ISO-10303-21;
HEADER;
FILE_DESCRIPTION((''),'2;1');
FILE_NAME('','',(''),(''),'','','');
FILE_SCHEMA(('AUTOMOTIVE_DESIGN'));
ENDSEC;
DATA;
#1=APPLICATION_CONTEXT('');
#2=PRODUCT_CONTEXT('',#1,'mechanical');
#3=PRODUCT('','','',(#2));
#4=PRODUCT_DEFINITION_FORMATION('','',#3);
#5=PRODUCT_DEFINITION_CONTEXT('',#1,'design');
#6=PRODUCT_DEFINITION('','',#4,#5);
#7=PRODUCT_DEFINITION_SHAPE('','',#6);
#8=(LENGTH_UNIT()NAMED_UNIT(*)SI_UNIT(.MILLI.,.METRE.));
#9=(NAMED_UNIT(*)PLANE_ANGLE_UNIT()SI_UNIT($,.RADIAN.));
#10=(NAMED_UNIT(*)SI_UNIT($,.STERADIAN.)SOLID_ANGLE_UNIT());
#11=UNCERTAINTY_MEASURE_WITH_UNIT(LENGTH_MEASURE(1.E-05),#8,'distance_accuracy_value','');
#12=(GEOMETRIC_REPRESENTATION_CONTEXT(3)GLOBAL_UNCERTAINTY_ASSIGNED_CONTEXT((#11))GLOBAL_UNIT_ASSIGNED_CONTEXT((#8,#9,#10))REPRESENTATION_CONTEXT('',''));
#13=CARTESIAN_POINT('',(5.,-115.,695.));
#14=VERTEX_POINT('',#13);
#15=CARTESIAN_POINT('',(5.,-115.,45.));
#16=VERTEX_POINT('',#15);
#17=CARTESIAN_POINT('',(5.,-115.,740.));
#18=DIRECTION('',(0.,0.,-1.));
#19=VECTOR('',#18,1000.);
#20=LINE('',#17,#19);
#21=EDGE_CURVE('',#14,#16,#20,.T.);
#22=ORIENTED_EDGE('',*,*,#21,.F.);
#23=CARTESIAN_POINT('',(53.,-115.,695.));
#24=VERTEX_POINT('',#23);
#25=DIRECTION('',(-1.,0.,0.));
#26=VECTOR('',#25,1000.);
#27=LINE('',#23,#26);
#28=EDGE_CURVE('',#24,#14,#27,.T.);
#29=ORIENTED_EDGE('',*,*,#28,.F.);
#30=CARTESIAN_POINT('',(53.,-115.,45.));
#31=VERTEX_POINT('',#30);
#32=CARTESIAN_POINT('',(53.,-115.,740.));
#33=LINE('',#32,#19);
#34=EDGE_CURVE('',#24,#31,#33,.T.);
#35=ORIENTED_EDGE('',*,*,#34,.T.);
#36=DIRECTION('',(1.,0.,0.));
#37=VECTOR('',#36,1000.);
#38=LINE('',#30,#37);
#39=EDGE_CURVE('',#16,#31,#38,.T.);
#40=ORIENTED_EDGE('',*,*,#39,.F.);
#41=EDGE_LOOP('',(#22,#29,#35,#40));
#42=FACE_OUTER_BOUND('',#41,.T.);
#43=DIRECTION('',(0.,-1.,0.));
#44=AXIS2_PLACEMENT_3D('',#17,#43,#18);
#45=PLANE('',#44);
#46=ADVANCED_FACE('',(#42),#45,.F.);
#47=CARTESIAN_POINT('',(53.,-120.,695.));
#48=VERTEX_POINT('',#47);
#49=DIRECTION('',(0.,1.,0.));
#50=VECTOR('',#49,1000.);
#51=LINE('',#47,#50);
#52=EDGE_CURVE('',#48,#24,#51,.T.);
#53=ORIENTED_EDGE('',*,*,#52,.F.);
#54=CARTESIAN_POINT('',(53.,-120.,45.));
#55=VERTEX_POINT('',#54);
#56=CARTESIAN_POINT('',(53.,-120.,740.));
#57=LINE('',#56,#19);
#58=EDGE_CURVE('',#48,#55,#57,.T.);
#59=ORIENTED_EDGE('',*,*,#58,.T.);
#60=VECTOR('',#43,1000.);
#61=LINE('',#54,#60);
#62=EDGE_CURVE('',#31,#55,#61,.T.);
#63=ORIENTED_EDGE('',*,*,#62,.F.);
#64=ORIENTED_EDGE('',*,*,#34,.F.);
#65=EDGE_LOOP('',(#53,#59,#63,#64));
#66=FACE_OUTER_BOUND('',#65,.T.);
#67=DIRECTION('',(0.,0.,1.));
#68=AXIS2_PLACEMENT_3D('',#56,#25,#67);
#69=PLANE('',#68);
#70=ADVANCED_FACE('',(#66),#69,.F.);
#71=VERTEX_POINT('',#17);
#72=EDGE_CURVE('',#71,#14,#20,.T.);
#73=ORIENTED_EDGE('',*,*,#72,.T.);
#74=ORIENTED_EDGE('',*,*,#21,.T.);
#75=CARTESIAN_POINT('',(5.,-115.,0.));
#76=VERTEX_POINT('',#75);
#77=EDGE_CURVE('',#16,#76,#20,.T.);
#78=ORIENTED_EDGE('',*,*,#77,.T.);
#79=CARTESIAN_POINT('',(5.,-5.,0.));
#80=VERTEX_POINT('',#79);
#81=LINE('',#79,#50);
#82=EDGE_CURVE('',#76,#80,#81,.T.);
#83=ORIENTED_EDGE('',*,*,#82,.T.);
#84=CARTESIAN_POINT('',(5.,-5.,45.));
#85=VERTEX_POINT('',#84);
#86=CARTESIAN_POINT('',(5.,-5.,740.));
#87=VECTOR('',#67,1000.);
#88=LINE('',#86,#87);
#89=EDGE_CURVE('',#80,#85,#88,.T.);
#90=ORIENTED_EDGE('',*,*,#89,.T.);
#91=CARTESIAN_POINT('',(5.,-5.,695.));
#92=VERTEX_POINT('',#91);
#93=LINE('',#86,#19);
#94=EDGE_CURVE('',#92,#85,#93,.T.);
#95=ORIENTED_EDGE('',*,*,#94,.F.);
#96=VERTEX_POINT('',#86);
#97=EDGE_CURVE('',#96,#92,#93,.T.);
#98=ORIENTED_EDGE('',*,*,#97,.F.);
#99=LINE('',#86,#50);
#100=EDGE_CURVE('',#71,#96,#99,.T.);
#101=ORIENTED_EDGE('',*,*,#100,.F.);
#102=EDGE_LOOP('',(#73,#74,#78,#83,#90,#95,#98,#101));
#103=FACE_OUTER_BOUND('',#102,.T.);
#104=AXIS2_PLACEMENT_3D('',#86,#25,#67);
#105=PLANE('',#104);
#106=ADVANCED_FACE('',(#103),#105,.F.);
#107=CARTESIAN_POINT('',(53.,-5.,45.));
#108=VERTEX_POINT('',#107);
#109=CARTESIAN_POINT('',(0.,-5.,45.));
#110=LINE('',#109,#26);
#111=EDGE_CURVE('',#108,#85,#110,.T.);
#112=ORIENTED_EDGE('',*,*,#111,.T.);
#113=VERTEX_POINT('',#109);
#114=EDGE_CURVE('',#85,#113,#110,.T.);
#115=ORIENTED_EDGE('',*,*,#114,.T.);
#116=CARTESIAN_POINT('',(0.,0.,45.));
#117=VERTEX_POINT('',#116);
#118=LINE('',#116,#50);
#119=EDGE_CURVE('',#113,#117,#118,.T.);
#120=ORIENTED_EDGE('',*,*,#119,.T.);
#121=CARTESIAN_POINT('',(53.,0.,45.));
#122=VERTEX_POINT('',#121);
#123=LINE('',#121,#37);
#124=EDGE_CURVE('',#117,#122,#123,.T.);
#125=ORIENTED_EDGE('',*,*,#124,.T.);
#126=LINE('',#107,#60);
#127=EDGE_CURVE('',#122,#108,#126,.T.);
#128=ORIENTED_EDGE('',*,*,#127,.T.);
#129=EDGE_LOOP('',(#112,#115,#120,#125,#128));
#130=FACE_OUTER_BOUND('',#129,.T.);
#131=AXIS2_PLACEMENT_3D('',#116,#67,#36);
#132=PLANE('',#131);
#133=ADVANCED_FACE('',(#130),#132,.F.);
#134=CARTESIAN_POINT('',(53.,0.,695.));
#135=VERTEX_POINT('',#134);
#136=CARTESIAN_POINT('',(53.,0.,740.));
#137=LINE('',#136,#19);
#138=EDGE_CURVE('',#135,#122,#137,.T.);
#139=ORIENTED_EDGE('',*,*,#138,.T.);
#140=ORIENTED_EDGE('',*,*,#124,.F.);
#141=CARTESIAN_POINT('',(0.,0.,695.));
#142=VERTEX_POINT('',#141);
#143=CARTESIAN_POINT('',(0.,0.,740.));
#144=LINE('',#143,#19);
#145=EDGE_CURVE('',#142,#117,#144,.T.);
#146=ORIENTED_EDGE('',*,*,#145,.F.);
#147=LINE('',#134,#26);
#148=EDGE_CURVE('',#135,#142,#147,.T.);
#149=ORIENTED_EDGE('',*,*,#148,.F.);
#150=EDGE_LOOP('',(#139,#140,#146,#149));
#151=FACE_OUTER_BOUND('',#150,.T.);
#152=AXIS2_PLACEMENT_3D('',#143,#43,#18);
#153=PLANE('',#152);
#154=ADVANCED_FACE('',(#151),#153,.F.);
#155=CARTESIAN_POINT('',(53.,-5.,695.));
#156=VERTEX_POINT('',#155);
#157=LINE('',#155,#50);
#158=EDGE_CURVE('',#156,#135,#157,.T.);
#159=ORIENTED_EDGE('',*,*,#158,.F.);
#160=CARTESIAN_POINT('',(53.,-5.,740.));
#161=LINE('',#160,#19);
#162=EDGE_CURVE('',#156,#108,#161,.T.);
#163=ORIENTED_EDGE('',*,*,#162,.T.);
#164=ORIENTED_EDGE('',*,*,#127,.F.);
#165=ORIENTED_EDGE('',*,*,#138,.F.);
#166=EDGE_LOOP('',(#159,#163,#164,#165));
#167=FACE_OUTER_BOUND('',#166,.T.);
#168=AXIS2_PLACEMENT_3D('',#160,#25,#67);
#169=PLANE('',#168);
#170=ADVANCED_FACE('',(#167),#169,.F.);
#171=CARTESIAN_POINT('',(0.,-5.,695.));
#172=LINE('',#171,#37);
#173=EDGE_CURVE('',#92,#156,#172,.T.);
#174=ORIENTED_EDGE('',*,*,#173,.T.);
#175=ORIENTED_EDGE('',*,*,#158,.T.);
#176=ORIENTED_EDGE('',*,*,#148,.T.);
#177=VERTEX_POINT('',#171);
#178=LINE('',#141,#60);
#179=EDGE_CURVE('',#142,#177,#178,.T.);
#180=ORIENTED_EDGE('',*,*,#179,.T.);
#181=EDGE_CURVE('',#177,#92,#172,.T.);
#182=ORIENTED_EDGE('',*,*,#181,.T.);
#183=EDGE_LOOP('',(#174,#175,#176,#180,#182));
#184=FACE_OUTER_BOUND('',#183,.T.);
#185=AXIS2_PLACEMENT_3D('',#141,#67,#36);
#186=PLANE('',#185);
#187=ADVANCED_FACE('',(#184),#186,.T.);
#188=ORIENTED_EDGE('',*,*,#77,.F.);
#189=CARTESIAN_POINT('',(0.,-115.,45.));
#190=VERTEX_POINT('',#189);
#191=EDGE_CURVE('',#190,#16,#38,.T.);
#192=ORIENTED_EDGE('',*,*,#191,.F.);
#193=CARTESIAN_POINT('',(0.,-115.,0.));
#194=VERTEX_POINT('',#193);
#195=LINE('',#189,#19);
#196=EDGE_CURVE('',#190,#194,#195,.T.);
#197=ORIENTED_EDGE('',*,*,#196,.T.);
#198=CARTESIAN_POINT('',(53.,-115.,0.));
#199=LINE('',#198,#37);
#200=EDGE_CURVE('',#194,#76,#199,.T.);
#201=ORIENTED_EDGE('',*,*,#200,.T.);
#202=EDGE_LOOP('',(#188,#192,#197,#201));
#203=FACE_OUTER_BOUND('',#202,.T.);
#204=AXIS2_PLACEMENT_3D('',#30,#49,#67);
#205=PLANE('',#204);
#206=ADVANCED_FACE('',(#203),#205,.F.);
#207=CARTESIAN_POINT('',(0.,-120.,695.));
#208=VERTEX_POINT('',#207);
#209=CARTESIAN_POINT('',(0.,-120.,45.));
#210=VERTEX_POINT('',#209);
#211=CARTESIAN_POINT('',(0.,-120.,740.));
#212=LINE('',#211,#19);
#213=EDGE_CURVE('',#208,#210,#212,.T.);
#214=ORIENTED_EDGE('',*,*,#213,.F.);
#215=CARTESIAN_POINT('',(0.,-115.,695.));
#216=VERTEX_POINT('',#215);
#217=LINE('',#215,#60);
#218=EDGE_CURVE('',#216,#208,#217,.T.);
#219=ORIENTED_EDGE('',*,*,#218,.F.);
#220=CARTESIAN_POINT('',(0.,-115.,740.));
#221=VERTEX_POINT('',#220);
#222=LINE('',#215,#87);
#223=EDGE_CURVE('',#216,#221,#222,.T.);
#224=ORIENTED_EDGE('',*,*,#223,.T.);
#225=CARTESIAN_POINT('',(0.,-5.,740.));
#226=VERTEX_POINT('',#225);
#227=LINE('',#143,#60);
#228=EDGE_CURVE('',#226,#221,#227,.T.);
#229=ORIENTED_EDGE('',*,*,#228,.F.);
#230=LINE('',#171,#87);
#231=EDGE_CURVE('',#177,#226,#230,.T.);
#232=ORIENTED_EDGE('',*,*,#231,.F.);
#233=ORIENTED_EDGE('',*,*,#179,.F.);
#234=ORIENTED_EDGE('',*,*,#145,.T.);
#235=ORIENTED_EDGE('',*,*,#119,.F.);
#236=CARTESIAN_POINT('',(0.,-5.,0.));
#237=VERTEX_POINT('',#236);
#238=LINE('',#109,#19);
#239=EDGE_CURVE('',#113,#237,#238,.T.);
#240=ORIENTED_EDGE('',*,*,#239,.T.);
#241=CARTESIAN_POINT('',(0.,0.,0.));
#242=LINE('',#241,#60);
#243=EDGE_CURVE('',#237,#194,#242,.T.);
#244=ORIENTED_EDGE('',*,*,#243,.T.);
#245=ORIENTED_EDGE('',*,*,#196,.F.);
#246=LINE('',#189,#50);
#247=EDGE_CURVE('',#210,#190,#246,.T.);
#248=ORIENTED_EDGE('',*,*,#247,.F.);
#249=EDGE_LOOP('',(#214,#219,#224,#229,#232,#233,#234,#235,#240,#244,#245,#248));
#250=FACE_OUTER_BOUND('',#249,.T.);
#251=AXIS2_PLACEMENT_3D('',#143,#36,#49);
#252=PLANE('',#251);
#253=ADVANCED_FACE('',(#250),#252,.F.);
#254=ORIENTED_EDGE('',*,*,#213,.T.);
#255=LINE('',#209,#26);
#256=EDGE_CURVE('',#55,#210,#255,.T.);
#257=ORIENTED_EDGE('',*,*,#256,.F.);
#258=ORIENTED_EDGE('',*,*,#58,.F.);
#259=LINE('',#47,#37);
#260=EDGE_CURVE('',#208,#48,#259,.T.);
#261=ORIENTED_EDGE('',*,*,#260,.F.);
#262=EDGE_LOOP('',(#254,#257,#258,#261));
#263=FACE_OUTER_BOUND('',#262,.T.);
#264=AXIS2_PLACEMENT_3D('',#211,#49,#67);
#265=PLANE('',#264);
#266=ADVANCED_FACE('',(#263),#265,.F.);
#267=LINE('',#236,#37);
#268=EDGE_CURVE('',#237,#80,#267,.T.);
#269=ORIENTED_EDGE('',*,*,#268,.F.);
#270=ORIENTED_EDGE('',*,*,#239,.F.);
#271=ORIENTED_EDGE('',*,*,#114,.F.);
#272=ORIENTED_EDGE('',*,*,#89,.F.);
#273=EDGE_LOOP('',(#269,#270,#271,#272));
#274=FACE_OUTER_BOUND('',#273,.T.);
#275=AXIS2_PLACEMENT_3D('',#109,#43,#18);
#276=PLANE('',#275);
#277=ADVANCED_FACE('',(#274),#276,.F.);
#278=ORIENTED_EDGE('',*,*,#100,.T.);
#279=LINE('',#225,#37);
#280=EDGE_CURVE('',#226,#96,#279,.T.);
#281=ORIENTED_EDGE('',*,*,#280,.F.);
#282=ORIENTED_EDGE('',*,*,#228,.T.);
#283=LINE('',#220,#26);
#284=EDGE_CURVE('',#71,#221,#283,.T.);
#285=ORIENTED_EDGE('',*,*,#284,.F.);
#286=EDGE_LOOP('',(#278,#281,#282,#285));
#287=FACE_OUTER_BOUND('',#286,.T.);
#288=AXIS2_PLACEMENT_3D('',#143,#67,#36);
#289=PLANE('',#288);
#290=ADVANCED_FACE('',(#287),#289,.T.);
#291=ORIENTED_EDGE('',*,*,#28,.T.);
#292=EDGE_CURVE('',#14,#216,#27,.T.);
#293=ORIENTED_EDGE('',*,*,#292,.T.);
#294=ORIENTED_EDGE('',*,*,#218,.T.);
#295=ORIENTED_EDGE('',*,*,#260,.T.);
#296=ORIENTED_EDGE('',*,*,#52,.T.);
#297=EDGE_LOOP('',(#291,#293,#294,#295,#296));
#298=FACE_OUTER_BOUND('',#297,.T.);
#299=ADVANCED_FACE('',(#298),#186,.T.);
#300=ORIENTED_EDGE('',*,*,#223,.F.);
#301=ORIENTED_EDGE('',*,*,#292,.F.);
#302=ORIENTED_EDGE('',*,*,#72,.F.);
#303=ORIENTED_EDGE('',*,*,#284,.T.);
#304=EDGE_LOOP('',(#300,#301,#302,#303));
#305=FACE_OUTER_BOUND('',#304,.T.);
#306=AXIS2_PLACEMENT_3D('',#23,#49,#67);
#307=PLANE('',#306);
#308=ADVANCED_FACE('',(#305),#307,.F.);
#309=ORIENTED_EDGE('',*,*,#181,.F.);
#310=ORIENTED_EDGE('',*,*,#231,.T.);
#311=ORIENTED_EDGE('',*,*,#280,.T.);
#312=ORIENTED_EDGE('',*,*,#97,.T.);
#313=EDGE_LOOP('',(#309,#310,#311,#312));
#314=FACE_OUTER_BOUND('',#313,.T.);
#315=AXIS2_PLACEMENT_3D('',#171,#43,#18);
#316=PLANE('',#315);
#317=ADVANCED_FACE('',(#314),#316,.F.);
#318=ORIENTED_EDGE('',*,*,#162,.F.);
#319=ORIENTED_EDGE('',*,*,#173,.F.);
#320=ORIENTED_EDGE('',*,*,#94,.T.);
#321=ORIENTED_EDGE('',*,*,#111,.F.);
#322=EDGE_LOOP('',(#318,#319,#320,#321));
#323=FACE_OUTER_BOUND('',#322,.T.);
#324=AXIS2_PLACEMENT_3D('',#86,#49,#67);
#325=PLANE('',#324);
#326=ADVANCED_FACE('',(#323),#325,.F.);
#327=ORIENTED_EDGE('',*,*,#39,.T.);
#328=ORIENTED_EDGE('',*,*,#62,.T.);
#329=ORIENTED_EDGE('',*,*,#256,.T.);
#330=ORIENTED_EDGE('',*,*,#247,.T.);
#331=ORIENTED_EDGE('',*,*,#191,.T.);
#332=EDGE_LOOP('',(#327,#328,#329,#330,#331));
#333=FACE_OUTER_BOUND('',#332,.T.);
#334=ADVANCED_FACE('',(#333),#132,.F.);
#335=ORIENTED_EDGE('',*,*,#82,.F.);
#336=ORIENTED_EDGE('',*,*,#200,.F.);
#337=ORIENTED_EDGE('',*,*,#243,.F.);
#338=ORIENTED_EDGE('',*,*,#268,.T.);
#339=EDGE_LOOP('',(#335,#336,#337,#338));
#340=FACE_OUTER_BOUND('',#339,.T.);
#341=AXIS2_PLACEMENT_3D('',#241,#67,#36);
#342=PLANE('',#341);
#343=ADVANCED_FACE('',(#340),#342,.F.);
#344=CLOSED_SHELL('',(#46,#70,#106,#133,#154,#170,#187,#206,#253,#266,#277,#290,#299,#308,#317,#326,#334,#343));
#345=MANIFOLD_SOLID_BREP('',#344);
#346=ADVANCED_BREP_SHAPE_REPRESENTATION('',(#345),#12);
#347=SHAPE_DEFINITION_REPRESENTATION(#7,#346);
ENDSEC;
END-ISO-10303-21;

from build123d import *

# Parameters (mm, degrees)
EXTRUDE_1_DEPTH     = 740
SKETCH_2_W          = 53
SKETCH_2_H          = 5
CUT_EXTRUDE_1_DEPTH = 45
SKETCH_3_W          = 53
SKETCH_3_H          = 5
CUT_EXTRUDE_2_DEPTH = 45
SKETCH_4_W          = 53
SKETCH_4_H          = 5
CUT_EXTRUDE_3_DEPTH = 45


with BuildPart() as part:
    # 草图1 → 凸台-拉伸1 (new body)
    with BuildSketch(Plane.XY):
        Polygon((0, 0), (0, -120), (53, -120), (53, -115), (5, -115), (5, -5), (53, -5), (53, 0), align=None)
    extrude(amount=EXTRUDE_1_DEPTH)

    # 草图2 → 切除-拉伸1 (cut)
    with BuildSketch(Plane(origin=(0, 0, 0), x_dir=(-1, 0, 0), z_dir=(0, 0, -1))):
        with Locations((-26.5, -2.5)):
            Rectangle(SKETCH_2_W, SKETCH_2_H)
    extrude(amount=-CUT_EXTRUDE_1_DEPTH, mode=Mode.SUBTRACT)

    # 草图3 → 切除-拉伸2 (cut)
    with BuildSketch(Plane(origin=(0, 0, 0), x_dir=(-1, 0, 0), z_dir=(0, 0, -1))):
        with Locations((-26.5, -117.5)):
            Rectangle(SKETCH_3_W, SKETCH_3_H)
    extrude(amount=-CUT_EXTRUDE_2_DEPTH, mode=Mode.SUBTRACT)

    # 草图4 → 切除-拉伸3 (cut)
    with BuildSketch(Plane.XY.offset(740)):
        with Locations((26.5, -2.5)):
            Rectangle(SKETCH_4_W, SKETCH_4_H)
        with Locations((26.5, -117.5)):
            Rectangle(SKETCH_4_W, SKETCH_4_H)
    extrude(amount=-CUT_EXTRUDE_3_DEPTH, mode=Mode.SUBTRACT)


solid = part.part
